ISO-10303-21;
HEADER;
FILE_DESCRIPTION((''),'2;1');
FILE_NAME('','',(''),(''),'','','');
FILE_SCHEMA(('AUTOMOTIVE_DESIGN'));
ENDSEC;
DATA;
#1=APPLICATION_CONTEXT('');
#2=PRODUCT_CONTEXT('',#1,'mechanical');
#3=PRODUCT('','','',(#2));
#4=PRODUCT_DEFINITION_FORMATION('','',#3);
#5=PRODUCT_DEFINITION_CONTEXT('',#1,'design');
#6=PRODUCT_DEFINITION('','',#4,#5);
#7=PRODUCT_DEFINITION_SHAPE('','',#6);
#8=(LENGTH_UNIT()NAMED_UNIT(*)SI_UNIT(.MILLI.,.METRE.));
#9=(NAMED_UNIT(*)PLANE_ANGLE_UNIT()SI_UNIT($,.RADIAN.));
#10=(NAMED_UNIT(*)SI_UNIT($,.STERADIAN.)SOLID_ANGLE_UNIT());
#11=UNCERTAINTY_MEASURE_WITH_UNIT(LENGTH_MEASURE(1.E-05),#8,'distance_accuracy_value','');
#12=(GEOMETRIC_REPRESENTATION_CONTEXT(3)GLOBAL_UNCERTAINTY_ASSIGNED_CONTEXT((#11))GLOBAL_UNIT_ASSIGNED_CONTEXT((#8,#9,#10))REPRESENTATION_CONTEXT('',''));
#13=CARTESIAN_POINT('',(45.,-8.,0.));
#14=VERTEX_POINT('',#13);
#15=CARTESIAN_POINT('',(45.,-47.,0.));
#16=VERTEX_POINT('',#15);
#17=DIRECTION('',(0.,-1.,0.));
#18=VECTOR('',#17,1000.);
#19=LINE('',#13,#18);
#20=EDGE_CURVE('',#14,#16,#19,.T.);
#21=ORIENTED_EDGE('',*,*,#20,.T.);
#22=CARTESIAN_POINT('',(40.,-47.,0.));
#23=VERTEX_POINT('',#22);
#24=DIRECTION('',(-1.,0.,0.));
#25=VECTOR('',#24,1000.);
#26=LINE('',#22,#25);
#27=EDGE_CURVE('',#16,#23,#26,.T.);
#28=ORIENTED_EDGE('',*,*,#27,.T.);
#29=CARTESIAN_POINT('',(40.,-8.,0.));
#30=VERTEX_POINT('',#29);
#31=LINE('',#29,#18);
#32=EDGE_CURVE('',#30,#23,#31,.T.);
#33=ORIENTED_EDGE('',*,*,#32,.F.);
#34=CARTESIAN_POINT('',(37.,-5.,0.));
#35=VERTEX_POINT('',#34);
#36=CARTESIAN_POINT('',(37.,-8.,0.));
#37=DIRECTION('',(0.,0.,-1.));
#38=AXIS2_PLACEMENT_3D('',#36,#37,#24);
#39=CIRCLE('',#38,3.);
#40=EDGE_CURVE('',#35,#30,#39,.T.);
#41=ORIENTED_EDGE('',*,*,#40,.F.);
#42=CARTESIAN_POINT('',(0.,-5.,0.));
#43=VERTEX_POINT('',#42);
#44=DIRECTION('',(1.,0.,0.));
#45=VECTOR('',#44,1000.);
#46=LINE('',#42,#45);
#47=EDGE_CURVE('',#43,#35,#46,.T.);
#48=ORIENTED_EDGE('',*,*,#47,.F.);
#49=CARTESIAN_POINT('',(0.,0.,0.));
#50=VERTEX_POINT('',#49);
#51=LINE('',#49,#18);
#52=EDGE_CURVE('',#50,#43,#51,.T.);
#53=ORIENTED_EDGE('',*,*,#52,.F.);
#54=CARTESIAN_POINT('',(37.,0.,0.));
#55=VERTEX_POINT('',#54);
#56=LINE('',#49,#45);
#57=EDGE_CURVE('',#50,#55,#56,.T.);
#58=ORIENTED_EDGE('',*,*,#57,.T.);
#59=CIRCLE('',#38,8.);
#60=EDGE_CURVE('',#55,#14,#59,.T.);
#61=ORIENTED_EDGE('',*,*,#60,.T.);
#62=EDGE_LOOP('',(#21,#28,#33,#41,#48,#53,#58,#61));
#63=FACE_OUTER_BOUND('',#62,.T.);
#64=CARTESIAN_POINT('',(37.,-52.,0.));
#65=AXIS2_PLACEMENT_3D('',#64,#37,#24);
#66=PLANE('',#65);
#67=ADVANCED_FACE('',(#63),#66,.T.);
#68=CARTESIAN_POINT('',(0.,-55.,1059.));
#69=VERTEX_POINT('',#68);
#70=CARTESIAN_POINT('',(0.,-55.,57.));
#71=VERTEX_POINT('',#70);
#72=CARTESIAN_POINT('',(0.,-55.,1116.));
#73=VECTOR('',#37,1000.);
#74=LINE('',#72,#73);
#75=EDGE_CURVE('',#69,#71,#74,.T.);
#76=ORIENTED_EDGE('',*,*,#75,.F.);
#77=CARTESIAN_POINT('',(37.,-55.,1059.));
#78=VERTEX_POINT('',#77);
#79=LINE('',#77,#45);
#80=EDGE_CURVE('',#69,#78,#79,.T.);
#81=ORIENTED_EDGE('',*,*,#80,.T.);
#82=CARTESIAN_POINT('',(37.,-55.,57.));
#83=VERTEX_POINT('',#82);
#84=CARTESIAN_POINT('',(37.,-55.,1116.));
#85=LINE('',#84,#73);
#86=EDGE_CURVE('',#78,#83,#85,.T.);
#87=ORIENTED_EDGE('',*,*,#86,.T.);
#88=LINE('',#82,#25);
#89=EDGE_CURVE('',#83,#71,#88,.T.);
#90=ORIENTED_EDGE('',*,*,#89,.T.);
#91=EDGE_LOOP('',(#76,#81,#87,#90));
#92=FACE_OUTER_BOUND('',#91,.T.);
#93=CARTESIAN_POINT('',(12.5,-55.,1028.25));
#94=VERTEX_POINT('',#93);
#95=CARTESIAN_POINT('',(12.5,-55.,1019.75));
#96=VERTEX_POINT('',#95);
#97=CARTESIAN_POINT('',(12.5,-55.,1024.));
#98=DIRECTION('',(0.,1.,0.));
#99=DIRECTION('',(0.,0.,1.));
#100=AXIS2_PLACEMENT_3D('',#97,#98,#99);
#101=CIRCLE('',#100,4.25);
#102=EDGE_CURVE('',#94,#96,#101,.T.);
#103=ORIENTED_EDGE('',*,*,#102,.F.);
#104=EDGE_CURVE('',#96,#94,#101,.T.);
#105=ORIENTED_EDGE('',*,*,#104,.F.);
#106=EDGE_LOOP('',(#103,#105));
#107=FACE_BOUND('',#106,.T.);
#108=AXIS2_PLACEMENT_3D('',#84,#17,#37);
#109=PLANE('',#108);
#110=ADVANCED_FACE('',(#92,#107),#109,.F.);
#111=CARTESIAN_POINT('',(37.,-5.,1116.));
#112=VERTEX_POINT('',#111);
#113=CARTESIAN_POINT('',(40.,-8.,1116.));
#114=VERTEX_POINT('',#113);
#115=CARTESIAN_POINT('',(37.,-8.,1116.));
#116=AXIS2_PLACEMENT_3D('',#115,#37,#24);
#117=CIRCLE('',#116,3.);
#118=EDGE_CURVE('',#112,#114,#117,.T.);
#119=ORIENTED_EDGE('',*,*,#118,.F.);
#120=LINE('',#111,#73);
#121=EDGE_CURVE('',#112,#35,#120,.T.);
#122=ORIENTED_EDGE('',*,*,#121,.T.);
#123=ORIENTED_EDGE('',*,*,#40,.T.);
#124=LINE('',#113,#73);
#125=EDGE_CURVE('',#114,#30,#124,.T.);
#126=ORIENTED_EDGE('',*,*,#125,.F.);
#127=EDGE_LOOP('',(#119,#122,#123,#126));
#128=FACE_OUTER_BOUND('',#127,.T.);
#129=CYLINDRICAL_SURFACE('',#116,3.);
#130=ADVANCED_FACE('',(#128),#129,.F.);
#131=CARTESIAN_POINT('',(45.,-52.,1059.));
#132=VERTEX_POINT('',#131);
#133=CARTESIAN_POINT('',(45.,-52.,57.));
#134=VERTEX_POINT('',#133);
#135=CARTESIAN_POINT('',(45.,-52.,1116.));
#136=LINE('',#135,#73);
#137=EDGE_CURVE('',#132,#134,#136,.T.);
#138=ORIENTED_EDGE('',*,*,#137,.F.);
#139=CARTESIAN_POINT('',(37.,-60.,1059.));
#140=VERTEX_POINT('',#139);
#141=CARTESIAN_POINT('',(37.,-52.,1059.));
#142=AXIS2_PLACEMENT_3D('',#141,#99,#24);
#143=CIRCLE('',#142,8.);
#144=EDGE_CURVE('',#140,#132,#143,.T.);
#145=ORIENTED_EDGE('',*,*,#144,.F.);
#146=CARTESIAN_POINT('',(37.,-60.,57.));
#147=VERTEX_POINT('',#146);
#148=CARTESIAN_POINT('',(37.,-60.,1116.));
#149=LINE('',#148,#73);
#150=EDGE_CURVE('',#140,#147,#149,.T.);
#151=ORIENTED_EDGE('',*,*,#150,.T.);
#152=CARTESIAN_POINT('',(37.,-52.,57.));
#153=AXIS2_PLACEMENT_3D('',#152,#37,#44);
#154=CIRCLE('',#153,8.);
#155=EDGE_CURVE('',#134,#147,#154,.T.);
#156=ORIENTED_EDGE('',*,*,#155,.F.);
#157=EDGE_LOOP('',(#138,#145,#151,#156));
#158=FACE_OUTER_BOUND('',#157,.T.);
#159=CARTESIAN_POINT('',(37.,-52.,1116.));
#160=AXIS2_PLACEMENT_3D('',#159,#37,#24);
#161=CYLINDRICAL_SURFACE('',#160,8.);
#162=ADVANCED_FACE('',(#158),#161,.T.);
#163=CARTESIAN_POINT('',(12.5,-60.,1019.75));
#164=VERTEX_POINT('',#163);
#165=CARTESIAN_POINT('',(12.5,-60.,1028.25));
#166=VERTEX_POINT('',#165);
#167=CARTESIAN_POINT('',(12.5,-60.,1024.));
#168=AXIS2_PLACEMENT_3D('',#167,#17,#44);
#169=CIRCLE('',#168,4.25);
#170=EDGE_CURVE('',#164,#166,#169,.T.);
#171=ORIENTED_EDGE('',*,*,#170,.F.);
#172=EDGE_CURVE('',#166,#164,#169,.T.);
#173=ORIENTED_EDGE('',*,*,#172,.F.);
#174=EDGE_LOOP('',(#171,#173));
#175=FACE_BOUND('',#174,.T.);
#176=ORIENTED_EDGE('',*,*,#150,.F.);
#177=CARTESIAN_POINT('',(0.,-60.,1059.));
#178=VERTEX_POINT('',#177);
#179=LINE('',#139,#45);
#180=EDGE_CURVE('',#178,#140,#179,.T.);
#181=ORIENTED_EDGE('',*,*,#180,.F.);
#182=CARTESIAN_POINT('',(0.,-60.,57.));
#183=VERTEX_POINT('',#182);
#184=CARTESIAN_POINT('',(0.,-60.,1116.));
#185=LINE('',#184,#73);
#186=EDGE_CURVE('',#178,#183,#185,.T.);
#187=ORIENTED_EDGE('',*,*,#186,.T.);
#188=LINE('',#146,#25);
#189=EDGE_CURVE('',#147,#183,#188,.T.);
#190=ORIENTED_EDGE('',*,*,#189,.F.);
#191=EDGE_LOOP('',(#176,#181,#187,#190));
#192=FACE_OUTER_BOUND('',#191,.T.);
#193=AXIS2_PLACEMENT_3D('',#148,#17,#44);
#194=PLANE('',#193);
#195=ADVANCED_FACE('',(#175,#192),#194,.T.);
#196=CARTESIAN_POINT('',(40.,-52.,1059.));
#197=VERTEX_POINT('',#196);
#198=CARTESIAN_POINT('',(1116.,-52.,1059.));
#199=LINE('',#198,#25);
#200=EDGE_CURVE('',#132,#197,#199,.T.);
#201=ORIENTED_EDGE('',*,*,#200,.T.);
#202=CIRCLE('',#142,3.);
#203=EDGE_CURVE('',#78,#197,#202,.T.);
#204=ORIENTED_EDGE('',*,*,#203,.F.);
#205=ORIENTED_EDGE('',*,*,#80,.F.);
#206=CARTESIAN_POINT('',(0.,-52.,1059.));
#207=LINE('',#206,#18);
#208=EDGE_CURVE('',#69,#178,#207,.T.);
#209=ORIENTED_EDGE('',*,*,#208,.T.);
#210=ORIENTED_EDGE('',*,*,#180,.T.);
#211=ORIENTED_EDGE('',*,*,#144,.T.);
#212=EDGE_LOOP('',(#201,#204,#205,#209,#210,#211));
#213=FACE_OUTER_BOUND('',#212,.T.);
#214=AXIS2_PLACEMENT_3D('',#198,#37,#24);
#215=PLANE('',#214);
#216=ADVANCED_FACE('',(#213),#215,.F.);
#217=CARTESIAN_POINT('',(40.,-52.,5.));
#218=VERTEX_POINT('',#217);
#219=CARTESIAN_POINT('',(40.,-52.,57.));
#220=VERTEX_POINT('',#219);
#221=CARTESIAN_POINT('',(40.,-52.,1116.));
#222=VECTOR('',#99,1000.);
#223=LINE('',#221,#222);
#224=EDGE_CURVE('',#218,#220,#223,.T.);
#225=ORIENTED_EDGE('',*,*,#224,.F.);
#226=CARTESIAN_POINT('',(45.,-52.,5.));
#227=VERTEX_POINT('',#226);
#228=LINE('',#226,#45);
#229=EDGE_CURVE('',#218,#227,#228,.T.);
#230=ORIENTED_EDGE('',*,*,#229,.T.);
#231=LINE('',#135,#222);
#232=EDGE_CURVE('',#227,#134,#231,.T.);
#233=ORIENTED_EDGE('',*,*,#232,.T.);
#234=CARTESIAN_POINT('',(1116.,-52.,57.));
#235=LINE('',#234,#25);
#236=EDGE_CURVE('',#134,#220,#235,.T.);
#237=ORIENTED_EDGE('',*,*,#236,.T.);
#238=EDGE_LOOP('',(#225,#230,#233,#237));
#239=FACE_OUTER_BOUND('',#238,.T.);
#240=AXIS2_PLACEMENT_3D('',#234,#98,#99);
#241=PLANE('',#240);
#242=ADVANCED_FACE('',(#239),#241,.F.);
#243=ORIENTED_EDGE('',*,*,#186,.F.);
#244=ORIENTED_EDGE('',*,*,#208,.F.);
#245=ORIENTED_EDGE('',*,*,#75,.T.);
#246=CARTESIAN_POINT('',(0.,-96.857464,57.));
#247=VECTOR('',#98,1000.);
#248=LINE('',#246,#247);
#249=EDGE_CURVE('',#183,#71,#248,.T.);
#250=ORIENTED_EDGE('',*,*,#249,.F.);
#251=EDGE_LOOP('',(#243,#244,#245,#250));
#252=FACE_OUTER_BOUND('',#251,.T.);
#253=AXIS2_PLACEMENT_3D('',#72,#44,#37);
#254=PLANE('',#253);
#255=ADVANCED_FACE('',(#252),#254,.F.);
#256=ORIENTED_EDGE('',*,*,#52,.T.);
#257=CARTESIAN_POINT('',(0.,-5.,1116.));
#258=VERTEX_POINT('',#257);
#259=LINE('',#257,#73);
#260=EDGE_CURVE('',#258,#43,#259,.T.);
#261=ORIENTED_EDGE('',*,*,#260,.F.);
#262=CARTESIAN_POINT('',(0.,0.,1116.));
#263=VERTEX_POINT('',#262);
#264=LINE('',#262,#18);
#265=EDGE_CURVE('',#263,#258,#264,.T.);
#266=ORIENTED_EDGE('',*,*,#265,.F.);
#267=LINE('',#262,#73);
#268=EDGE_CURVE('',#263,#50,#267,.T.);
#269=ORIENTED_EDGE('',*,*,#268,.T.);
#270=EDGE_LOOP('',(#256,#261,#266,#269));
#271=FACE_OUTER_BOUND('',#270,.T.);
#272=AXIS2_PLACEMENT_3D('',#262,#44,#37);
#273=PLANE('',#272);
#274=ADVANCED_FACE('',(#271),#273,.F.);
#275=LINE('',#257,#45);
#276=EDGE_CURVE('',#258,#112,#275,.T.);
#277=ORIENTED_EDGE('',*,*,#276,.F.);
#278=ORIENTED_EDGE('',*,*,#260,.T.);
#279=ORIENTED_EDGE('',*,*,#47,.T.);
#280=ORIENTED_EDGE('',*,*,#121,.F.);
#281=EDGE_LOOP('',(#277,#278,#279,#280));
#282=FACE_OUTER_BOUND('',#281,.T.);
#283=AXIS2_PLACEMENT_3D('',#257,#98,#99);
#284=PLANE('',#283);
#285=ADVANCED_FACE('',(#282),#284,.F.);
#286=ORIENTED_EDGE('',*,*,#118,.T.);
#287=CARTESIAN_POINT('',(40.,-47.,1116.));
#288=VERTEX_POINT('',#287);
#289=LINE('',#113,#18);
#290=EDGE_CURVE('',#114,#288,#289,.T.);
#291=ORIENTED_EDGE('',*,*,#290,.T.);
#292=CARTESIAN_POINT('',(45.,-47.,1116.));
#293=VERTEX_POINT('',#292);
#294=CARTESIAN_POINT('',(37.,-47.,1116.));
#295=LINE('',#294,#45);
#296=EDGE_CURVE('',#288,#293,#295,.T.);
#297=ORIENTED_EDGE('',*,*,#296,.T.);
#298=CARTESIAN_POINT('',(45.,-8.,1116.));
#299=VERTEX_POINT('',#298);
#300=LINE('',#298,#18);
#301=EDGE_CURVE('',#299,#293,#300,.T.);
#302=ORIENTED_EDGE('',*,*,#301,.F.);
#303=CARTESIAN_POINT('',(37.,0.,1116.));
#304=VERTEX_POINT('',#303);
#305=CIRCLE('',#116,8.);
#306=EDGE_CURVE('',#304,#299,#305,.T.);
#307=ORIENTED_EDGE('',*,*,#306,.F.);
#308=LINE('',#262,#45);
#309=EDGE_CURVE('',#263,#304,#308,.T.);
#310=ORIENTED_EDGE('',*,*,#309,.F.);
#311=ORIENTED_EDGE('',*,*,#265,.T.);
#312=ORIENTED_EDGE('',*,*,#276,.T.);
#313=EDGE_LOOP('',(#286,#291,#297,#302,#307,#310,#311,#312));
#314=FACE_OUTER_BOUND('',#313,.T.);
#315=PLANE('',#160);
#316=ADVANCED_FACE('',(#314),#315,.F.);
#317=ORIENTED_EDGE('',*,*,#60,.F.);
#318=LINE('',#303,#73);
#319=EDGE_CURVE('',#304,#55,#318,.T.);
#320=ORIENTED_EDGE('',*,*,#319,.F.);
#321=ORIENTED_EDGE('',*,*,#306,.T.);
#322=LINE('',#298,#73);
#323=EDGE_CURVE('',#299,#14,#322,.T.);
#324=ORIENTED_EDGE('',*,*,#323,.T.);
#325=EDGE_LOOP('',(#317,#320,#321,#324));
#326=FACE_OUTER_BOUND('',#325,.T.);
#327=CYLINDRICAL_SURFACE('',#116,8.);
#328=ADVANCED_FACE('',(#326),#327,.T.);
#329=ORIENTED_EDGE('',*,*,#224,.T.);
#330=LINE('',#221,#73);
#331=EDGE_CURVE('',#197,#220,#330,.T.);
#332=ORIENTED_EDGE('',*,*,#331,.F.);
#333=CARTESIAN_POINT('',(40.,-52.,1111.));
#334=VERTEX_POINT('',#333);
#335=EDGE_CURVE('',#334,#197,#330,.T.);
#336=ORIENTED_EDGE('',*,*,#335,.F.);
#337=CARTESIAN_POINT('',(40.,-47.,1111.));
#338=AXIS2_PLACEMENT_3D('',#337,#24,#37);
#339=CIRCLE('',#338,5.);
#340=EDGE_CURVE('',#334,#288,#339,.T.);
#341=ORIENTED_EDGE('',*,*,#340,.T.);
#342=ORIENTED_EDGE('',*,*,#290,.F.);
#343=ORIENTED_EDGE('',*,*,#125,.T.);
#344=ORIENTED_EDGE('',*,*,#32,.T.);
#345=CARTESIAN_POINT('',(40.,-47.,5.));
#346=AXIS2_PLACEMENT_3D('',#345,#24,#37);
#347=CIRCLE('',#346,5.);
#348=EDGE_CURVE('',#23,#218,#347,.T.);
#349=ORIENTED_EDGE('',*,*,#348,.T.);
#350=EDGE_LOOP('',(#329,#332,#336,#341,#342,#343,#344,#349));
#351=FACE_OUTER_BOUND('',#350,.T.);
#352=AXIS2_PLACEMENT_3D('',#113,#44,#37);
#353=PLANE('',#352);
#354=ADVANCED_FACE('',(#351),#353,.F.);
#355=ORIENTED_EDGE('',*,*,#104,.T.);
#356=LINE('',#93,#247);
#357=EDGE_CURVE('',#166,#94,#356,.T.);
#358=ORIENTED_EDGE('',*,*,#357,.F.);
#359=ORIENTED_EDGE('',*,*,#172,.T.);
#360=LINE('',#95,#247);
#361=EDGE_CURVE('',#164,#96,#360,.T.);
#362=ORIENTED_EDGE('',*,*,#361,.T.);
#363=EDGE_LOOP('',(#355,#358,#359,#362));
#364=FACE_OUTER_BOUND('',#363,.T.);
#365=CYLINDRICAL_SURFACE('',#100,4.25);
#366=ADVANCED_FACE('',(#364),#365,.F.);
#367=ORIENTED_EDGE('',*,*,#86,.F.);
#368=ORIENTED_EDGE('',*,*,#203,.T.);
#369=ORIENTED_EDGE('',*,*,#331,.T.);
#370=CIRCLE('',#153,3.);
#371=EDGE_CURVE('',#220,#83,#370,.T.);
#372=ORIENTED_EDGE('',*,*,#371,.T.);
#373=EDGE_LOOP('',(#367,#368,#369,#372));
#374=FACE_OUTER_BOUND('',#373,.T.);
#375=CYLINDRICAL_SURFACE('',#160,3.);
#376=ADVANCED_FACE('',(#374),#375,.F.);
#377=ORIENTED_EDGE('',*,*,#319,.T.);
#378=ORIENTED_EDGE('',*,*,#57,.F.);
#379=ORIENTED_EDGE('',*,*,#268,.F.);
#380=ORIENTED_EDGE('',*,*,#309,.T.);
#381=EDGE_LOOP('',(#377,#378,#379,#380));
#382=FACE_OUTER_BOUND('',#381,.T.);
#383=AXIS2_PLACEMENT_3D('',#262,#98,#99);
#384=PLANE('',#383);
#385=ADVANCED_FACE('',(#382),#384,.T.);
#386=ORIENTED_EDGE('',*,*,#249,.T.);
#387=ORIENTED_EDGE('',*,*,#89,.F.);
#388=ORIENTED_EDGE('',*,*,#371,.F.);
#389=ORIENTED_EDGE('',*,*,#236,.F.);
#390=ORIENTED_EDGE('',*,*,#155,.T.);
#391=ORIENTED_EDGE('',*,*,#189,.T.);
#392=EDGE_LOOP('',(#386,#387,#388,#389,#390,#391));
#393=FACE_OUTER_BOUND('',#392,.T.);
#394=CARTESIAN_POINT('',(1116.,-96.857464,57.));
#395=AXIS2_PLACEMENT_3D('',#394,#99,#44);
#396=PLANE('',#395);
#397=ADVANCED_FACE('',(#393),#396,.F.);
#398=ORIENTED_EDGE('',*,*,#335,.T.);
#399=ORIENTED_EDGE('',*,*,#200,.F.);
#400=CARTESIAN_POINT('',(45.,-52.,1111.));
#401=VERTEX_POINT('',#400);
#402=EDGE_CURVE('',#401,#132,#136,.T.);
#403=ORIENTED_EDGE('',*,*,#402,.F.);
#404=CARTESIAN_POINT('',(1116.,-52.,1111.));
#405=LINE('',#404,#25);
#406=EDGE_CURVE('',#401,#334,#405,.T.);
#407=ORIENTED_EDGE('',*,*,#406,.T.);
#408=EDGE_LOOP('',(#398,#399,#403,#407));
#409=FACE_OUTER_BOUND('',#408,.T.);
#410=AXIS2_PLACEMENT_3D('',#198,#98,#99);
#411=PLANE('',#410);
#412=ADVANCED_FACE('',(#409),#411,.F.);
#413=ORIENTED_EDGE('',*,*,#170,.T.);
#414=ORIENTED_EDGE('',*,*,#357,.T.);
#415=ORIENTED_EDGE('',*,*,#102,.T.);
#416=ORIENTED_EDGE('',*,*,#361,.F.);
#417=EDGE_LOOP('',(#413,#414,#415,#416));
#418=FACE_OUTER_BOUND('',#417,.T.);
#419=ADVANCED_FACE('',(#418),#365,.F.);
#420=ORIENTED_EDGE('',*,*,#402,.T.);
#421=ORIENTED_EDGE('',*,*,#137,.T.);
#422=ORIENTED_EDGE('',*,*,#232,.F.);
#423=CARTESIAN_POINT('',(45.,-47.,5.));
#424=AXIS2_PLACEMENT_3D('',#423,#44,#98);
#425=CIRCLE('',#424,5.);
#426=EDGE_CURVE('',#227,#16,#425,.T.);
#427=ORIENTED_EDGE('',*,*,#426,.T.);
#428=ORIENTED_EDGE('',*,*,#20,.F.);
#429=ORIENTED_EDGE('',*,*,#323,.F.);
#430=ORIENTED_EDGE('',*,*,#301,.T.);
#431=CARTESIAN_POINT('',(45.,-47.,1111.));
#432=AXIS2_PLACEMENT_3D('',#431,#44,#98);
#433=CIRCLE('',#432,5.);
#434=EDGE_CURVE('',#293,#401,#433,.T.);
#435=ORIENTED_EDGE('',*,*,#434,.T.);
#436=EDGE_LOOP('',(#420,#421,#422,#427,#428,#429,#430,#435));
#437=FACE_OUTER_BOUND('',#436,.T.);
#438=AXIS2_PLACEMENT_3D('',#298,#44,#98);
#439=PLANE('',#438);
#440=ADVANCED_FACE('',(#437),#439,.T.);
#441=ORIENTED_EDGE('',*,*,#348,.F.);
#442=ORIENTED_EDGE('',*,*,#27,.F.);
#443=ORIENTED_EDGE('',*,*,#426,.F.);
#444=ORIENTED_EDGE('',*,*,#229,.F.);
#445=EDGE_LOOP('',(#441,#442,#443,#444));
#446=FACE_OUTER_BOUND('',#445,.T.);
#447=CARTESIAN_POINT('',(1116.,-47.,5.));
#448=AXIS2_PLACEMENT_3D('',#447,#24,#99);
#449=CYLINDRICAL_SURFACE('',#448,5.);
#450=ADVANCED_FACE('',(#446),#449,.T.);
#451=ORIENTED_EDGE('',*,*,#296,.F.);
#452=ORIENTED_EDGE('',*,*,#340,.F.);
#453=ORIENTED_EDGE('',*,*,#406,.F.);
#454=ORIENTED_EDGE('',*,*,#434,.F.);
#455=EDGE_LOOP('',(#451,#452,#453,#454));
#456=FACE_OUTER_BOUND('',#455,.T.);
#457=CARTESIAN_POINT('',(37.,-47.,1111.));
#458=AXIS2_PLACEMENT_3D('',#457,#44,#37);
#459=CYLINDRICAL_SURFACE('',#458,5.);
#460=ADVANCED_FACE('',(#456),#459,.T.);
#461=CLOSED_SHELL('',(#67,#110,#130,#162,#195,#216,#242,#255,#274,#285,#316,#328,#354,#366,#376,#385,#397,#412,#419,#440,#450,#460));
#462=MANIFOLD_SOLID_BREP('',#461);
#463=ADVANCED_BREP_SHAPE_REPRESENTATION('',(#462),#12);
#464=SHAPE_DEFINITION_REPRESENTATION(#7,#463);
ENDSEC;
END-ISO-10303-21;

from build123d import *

# Parameters (mm, degrees)
BOSS_EXTRUDE1_DEPTH    = 1116
SKETCH2_W              = 92.475127077
SKETCH2_H              = 38.646657261
SKETCH2_W_2            = 90.397253408
SKETCH2_H_2            = 44.857464027
CUT_EXTRUDE1_DEPTH     = 1116
SKETCH3_R              = 4
CUT_EXTRUDE2_DEPTH     = 1116
FILLET1_R              = 5
M10_TAPPED_HOLE1_D     = 8.5
M10_TAPPED_HOLE1_DEPTH = 24.5
M10_TAPPED_HOLE1_TIP   = 2.553657631


with BuildPart() as part:
    # Sketch1 → Boss-Extrude1 (new body)
    with BuildSketch(Plane.XY):
        with BuildLine():
            Line((0, 0), (37, 0))
            ThreePointArc((37, 0), (42.656854249, -2.343145751), (45, -8))
            Line((45, -8), (45, -52))
            ThreePointArc((45, -52), (42.656854249, -57.656854249), (37, -60))
            Line((37, -60), (0, -60))
            Line((0, -60), (0, -55))
            Line((0, -55), (37, -55))
            ThreePointArc((37, -55), (39.121320344, -54.121320344), (40, -52))
            Line((40, -52), (40, -8))
            ThreePointArc((40, -8), (39.121320344, -5.878679656), (37, -5))
            Line((37, -5), (0, -5))
            Line((0, -5), (0, 0))
        make_face()
    extrude(amount=BOSS_EXTRUDE1_DEPTH)

    # Sketch2 → Cut-Extrude1 (cut)
    with BuildSketch(Plane.ZY):
        with Locations((1105.237563539, -71.323328631)):
            Rectangle(SKETCH2_W, SKETCH2_H)
        with Locations((11.801373296, -74.428732013)):
            Rectangle(SKETCH2_W_2, SKETCH2_H_2)
    extrude(amount=-CUT_EXTRUDE1_DEPTH, mode=Mode.SUBTRACT)

    # Sketch3 → Cut-Extrude2 (cut)
    with BuildSketch(Plane(origin=(0, -55, 0), x_dir=(1, 0, 0), z_dir=(0, 1, 0))):
        with Locations(Location((12.5, -1024, 0), (0, 0, 270))):
            Circle(SKETCH3_R)
    extrude(amount=-CUT_EXTRUDE2_DEPTH, mode=Mode.SUBTRACT)

    # Fillet1
    fillet1_edges = [part.edges().sort_by_distance(p)[0] for p in [
        (42.5, -52, 0),
        (42.5, -52, 1116),
    ]]
    fillet(fillet1_edges, radius=FILLET1_R)

    # M10 Tapped Hole1
    with Locations(Plane(origin=(0, -55, 0), x_dir=(1, 0, 0), z_dir=(0, 1, 0))):
        with Locations((12.5, -1024)):
            Hole(M10_TAPPED_HOLE1_D / 2, depth=M10_TAPPED_HOLE1_DEPTH)
            with Locations((0, 0, -(M10_TAPPED_HOLE1_DEPTH + M10_TAPPED_HOLE1_TIP / 2))):  # 118° drill point
                Cone(0, M10_TAPPED_HOLE1_D / 2, M10_TAPPED_HOLE1_TIP, mode=Mode.SUBTRACT)


solid = part.part
